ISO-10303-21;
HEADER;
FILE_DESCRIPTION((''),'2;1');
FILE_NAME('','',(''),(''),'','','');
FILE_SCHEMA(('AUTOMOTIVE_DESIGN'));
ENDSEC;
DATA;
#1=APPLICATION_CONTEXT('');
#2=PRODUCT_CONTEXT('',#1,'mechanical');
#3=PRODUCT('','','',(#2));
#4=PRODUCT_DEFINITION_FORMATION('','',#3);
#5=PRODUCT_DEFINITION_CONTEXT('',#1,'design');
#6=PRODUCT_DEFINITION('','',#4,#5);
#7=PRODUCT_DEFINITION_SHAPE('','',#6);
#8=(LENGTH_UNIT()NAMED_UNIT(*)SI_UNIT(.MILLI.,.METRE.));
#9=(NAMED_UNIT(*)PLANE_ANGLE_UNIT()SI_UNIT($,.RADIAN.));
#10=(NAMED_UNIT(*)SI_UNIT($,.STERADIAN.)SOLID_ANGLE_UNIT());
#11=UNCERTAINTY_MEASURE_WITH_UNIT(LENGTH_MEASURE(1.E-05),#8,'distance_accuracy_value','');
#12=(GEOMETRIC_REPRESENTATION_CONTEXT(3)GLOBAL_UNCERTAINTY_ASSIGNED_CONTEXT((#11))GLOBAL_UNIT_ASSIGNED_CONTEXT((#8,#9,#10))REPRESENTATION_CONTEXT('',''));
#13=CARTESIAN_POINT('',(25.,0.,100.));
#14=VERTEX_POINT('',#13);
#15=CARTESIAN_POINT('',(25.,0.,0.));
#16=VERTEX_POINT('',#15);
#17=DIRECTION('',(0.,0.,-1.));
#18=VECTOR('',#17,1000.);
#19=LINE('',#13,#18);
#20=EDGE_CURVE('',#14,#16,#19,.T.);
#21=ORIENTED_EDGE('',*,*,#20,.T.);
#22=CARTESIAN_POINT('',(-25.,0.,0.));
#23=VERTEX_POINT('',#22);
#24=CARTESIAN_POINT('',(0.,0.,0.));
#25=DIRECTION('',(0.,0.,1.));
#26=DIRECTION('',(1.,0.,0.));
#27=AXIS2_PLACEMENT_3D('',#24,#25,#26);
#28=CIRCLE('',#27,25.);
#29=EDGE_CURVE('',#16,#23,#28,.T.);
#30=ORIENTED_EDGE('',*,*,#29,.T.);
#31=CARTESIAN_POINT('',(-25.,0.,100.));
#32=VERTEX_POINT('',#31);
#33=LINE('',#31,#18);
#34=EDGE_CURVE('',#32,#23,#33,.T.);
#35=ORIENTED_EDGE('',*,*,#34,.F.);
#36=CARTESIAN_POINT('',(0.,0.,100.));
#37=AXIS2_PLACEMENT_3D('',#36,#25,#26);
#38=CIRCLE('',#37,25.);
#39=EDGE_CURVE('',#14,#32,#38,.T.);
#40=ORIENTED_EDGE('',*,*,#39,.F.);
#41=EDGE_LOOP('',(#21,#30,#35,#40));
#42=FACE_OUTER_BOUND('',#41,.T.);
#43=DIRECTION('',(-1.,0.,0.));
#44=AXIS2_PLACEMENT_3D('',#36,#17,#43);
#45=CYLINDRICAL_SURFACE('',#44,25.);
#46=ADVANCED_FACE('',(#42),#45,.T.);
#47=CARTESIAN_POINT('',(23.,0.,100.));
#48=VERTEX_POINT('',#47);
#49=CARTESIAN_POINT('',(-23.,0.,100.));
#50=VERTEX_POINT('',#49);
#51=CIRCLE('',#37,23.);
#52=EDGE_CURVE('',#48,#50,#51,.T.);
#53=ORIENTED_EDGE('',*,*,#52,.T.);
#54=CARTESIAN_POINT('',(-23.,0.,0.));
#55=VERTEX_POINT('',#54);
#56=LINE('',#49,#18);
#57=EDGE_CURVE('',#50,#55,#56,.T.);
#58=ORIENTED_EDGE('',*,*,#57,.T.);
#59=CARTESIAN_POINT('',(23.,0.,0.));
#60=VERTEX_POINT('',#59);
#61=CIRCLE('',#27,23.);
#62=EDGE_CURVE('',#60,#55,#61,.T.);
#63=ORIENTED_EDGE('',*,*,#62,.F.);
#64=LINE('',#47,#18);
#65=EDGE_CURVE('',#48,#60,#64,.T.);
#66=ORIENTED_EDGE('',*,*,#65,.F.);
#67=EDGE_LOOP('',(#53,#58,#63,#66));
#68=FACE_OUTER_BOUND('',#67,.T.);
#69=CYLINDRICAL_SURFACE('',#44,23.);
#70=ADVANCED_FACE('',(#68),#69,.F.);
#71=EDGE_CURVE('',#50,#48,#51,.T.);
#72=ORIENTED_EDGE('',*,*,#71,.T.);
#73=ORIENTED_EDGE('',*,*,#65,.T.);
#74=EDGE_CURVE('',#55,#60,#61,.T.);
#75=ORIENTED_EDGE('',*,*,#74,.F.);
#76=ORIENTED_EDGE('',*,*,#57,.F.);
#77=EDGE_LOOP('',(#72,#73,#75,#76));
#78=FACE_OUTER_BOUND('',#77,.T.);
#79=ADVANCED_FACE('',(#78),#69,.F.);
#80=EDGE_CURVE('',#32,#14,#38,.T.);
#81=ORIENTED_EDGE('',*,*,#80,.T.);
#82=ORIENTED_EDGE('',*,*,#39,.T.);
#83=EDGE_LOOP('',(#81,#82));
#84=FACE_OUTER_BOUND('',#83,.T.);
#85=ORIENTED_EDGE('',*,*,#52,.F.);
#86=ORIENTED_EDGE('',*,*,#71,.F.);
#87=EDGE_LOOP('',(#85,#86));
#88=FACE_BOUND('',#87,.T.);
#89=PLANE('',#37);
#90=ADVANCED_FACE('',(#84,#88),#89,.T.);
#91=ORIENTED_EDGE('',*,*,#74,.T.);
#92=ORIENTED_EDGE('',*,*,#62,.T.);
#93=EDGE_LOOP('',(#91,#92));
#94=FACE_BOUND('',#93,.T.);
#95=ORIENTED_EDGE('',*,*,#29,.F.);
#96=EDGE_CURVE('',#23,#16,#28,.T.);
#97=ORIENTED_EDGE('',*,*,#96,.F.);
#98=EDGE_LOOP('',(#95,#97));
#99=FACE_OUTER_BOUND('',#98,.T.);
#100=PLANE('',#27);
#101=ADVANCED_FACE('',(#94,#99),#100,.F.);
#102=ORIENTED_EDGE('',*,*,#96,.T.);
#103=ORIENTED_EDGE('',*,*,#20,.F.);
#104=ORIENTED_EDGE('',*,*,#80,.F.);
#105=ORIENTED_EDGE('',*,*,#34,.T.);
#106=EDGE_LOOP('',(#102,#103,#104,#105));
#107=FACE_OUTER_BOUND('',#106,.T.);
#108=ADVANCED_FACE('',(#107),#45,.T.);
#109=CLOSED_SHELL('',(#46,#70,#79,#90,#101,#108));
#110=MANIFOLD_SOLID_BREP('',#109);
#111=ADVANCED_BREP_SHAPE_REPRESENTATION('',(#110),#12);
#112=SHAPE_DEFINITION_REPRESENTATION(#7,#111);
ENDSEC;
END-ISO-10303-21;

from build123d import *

# Parameters (mm, degrees)
SKETCH1_R           = 25
SKETCH1_R_2         = 23
BOSS_EXTRUDE1_DEPTH = 100


with BuildPart() as part:
    # Sketch1 → Boss-Extrude1 (new body)
    with BuildSketch(Plane.XY):
        Circle(SKETCH1_R)
        Circle(SKETCH1_R_2, mode=Mode.SUBTRACT)
    extrude(amount=BOSS_EXTRUDE1_DEPTH)


solid = part.part
